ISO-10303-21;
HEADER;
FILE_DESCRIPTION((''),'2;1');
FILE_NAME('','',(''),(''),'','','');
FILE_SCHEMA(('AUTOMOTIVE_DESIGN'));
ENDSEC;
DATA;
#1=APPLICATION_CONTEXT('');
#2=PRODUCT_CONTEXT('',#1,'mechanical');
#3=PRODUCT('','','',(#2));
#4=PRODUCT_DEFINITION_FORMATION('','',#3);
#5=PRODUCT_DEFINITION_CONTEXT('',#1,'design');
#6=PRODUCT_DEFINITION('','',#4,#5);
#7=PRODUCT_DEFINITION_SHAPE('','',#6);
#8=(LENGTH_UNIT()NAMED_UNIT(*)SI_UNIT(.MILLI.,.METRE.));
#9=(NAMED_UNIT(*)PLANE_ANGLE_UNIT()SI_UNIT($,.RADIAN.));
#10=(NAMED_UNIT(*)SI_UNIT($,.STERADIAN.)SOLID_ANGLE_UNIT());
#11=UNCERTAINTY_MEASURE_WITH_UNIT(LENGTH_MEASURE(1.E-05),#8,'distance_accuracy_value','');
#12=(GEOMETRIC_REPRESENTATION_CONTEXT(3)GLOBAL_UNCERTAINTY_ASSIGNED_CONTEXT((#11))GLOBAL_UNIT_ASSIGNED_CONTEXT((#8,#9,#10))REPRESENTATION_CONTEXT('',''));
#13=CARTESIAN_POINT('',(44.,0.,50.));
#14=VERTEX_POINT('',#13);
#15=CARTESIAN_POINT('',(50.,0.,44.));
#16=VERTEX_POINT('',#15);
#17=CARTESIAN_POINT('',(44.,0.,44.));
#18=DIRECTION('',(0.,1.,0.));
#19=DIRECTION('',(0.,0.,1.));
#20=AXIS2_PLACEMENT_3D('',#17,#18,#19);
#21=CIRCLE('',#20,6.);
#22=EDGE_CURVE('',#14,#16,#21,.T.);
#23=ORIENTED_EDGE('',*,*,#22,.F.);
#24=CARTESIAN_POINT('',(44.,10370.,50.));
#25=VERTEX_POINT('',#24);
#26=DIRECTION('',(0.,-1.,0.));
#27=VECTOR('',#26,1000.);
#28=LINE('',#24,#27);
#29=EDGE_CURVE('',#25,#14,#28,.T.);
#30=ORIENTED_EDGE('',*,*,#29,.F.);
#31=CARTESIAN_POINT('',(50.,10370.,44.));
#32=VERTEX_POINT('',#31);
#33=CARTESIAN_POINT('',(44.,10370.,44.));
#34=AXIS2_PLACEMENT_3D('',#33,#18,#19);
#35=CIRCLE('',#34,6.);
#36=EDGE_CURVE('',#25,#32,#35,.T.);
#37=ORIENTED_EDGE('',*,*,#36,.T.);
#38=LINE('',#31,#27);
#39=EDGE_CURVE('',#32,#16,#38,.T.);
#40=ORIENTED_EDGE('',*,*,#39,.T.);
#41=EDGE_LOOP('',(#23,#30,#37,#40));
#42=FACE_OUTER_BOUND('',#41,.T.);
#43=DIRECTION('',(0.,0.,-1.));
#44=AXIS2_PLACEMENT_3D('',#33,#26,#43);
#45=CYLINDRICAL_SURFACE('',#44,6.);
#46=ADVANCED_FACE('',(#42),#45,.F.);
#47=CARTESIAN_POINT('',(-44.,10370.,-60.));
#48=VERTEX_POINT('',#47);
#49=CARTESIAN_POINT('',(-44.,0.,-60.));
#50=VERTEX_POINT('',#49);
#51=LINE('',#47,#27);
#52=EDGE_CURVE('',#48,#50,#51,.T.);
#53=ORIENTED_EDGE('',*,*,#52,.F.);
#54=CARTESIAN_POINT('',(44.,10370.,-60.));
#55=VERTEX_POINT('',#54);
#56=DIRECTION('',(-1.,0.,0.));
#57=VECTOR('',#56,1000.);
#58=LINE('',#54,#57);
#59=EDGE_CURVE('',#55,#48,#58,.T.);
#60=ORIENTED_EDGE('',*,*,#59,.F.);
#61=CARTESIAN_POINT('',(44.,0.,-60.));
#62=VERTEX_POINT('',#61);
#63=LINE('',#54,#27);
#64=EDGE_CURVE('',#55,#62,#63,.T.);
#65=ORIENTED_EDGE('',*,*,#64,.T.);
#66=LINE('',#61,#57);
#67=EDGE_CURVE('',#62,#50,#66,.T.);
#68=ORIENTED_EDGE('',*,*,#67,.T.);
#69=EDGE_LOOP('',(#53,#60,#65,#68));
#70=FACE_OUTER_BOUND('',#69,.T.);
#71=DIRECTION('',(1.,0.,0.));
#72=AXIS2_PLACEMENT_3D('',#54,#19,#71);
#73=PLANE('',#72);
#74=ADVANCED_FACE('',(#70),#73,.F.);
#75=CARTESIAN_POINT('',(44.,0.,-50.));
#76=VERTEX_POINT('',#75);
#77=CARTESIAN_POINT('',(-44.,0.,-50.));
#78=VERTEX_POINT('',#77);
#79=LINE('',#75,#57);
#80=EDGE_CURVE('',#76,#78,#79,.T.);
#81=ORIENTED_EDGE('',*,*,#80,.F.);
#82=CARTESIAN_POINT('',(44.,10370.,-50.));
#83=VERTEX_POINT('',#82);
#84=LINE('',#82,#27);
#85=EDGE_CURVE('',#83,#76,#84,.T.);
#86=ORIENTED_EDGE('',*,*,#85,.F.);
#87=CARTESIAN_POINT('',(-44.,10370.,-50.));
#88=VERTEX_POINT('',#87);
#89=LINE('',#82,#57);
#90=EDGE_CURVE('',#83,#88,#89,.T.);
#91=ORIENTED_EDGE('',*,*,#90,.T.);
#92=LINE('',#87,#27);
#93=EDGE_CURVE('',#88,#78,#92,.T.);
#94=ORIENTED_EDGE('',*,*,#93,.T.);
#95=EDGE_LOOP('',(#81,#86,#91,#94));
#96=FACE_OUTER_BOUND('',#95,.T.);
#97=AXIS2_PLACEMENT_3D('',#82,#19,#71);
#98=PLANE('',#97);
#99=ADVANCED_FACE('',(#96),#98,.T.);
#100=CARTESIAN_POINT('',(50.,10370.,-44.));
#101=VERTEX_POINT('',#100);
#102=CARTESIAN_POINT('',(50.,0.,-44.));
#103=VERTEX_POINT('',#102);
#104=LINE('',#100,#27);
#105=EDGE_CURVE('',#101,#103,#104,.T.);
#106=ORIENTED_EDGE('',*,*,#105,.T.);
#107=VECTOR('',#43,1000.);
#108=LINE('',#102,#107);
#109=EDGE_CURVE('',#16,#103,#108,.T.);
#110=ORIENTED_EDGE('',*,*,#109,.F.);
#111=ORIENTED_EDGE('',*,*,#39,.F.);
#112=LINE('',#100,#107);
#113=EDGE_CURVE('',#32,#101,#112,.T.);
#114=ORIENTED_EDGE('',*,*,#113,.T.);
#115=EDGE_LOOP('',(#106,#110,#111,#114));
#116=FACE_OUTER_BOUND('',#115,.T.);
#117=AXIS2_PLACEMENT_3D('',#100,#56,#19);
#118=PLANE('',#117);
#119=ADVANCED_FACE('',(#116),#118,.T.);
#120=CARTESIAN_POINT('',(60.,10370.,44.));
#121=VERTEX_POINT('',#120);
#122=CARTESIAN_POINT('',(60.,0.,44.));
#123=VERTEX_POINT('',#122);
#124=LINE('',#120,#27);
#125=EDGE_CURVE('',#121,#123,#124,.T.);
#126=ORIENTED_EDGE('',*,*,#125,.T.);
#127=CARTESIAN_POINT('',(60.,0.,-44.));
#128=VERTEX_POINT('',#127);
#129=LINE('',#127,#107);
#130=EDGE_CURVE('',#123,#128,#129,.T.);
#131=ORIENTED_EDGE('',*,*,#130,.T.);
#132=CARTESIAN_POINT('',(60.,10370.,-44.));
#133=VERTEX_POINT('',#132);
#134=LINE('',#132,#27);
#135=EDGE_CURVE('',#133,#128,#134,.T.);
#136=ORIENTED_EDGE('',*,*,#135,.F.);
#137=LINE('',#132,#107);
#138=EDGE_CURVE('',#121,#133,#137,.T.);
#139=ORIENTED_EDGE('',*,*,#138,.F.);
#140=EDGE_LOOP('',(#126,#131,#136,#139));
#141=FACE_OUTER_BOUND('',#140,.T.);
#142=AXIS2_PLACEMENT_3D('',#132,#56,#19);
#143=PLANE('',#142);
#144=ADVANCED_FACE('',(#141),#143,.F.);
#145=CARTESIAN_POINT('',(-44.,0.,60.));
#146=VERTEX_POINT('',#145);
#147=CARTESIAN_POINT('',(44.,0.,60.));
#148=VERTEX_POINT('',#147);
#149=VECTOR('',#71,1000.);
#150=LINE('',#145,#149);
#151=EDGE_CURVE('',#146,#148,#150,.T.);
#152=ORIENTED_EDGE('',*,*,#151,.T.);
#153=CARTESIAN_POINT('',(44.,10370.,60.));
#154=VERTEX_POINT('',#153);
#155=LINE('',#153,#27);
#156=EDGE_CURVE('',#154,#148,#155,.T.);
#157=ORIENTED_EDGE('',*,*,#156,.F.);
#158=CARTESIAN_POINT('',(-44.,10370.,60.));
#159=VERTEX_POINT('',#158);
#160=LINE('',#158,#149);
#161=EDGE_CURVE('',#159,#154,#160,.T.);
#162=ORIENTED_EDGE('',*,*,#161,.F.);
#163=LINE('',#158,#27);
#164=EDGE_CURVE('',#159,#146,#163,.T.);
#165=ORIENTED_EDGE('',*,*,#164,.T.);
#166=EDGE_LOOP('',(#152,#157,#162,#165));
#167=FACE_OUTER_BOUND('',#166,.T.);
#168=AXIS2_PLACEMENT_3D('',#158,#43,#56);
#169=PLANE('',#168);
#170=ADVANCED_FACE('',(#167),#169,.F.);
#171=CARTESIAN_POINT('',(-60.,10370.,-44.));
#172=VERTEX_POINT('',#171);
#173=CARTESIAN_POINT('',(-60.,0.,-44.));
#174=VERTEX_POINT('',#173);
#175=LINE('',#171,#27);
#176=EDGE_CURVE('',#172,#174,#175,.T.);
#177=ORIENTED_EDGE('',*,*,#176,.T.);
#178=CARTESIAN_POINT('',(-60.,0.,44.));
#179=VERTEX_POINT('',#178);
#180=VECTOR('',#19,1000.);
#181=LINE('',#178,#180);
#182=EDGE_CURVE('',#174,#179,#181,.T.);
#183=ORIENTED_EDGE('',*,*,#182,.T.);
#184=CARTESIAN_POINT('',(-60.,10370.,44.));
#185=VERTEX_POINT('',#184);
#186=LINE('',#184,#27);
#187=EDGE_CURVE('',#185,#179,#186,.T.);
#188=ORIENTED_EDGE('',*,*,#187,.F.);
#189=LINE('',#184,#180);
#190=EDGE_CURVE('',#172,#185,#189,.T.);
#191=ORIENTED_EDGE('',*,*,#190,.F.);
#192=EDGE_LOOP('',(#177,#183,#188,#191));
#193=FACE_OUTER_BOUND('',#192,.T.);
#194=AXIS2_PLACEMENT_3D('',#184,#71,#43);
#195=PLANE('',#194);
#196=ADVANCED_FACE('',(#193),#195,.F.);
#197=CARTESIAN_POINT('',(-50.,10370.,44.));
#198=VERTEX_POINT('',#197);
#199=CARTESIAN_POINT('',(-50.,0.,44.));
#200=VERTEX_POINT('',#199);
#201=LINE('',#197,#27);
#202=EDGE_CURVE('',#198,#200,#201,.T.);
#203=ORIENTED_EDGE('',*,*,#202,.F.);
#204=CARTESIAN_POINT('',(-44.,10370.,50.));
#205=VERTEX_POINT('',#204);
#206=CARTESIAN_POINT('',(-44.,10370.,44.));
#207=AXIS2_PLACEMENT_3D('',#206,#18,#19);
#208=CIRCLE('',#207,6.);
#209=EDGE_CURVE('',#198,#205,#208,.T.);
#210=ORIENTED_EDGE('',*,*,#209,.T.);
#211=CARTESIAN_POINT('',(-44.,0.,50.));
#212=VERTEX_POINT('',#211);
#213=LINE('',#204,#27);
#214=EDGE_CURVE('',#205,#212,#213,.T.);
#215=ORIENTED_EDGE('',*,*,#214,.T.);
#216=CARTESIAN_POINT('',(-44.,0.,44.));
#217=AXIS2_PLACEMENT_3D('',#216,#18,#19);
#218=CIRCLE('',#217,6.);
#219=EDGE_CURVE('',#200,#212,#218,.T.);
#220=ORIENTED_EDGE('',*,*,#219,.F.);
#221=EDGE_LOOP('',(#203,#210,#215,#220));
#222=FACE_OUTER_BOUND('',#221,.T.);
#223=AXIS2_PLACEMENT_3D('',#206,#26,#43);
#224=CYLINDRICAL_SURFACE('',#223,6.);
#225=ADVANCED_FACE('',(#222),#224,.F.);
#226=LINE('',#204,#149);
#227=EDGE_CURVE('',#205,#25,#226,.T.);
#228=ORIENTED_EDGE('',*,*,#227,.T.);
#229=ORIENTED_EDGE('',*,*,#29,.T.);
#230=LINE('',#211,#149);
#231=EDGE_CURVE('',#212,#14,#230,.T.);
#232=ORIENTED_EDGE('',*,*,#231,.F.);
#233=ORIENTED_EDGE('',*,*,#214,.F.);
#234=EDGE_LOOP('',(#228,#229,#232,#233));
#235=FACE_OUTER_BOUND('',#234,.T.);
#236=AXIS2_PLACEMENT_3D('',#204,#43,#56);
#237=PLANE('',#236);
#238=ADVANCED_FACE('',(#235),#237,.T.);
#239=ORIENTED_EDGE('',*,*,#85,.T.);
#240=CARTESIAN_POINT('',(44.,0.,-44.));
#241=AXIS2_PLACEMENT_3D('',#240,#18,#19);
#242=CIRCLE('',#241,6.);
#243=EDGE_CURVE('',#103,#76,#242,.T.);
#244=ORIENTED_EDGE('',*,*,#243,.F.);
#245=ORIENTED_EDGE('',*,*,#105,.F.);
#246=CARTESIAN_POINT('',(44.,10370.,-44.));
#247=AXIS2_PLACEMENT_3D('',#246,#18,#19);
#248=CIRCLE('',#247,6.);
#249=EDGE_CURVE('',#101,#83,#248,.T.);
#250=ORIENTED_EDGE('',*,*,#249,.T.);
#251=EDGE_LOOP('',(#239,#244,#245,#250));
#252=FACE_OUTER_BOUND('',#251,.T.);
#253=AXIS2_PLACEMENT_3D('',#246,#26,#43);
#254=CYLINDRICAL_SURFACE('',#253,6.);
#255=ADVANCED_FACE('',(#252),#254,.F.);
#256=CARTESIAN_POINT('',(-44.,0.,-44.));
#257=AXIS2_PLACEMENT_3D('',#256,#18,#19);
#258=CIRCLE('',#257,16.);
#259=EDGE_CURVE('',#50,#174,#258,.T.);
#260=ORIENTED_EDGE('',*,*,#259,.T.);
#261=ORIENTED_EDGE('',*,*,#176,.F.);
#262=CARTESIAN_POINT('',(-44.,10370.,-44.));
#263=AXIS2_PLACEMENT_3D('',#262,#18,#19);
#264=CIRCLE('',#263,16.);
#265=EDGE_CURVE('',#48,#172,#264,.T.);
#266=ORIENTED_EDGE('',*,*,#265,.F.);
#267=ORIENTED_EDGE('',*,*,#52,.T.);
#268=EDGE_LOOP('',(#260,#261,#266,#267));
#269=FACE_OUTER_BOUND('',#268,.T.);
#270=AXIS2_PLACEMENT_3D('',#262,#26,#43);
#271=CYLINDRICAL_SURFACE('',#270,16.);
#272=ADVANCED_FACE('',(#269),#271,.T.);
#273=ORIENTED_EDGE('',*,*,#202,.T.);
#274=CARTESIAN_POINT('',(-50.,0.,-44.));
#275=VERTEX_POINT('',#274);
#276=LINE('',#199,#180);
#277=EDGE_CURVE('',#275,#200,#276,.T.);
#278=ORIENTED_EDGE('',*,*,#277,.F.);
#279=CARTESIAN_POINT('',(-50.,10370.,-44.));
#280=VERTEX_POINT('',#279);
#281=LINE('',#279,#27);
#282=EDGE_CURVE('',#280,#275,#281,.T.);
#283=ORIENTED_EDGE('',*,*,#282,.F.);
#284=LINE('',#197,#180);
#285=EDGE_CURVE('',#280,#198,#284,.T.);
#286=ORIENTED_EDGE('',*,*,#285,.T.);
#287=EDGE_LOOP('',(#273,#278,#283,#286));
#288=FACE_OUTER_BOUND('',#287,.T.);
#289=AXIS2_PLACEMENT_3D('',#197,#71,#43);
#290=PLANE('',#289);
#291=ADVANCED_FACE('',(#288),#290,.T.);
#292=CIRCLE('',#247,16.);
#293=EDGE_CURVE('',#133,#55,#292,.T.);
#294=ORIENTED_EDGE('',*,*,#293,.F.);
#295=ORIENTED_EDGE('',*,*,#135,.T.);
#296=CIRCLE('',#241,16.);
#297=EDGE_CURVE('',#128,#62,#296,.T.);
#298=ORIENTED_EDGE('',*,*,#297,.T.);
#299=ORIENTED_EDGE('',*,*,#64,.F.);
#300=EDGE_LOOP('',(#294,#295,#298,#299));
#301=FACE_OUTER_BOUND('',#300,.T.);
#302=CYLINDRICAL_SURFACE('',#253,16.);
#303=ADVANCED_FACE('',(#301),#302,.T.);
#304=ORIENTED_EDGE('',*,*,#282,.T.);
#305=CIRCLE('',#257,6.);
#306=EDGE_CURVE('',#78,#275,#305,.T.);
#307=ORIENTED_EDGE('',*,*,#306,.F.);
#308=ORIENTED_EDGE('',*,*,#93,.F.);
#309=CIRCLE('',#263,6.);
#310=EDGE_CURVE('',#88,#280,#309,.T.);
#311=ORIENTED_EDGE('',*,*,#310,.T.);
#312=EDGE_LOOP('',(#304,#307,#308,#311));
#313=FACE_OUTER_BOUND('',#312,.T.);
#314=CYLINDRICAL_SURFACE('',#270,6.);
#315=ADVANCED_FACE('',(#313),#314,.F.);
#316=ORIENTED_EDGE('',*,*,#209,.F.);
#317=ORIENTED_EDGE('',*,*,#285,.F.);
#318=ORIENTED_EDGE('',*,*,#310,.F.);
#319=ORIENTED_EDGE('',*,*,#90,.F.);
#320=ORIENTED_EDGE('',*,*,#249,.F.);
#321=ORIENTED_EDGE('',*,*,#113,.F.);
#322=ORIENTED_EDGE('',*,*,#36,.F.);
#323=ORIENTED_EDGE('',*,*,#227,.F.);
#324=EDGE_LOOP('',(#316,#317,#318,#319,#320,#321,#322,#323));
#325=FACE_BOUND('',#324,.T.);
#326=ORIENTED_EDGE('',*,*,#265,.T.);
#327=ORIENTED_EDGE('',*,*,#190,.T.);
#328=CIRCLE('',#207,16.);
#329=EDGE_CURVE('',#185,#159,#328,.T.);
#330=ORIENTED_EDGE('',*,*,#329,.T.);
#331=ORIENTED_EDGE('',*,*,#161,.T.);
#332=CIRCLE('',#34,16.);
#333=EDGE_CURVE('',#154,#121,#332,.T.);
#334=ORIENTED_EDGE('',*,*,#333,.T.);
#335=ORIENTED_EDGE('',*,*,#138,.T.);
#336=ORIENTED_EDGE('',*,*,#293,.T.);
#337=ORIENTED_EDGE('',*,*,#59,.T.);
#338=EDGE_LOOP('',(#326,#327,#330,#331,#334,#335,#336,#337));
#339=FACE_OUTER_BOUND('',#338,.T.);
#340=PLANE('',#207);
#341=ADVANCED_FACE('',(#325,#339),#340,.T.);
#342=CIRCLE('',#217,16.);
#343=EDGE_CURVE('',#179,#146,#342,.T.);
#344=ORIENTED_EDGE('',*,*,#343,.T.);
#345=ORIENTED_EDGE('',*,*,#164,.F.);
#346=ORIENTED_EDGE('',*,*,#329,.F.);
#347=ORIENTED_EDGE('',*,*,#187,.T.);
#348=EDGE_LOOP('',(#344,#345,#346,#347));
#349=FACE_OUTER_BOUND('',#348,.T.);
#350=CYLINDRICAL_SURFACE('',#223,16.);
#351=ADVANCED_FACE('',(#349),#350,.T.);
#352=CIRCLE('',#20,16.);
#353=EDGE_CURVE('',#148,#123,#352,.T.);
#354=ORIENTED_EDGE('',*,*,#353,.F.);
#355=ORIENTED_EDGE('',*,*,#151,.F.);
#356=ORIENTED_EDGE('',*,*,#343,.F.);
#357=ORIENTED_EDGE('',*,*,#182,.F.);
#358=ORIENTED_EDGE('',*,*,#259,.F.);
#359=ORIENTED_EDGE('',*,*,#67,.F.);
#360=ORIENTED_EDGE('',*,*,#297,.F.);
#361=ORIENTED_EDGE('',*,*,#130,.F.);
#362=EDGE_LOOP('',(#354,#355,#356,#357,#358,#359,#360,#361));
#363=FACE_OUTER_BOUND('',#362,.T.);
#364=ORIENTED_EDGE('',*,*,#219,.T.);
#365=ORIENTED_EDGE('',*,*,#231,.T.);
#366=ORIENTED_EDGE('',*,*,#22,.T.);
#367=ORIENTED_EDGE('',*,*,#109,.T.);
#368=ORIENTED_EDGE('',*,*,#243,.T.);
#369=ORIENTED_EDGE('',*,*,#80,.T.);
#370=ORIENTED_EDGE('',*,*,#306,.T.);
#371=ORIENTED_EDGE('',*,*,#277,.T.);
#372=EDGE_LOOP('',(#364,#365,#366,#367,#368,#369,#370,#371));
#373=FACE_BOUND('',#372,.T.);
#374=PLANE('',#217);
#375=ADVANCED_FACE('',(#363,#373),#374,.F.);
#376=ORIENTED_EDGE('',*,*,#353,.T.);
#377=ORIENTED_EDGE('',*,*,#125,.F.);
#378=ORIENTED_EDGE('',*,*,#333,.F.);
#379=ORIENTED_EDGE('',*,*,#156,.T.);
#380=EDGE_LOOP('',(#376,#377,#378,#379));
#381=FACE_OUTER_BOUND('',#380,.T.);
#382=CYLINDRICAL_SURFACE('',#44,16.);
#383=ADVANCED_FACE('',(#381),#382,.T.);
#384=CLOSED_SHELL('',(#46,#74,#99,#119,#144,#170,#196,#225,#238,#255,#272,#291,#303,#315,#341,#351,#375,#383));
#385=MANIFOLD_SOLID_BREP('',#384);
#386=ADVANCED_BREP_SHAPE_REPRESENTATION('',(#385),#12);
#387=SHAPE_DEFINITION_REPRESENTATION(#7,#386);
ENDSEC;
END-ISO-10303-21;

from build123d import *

# Parameters (mm, degrees)
COLD_FORMED_HOLLOW_STRUCTURAL_SQUARE_STE_DEPTH = 10370


with BuildPart() as part:
    # Sketch12 → Cold-formed Hollow Structural Square Steel(gb t6728-2002) 120×120×10(1) (new body)
    with BuildSketch(Plane(origin=(0, 0, 0), x_dir=(-1, 0, 0), z_dir=(0, 1, 0))):
        with BuildLine():
            Line((-44, -60), (44, -60))
            ThreePointArc((44, -60), (55.313708499, -55.313708499), (60, -44))
            Line((60, -44), (60, 44))
            ThreePointArc((60, 44), (55.313708499, 55.313708499), (44, 60))
            Line((44, 60), (-44, 60))
            ThreePointArc((-44, 60), (-55.313708499, 55.313708499), (-60, 44))
            Line((-60, 44), (-60, -44))
            ThreePointArc((-60, -44), (-55.313708499, -55.313708499), (-44, -60))
        make_face()
        with BuildLine():
            Line((-44, -50), (44, -50))
            ThreePointArc((44, -50), (48.242640687, -48.242640687), (50, -44))
            Line((50, -44), (50, 44))
            ThreePointArc((50, 44), (48.242640687, 48.242640687), (44, 50))
            Line((44, 50), (-44, 50))
            ThreePointArc((-44, 50), (-48.242640687, 48.242640687), (-50, 44))
            Line((-50, 44), (-50, -44))
            ThreePointArc((-50, -44), (-48.242640687, -48.242640687), (-44, -50))
        make_face(mode=Mode.SUBTRACT)
    extrude(amount=COLD_FORMED_HOLLOW_STRUCTURAL_SQUARE_STE_DEPTH)


solid = part.part
